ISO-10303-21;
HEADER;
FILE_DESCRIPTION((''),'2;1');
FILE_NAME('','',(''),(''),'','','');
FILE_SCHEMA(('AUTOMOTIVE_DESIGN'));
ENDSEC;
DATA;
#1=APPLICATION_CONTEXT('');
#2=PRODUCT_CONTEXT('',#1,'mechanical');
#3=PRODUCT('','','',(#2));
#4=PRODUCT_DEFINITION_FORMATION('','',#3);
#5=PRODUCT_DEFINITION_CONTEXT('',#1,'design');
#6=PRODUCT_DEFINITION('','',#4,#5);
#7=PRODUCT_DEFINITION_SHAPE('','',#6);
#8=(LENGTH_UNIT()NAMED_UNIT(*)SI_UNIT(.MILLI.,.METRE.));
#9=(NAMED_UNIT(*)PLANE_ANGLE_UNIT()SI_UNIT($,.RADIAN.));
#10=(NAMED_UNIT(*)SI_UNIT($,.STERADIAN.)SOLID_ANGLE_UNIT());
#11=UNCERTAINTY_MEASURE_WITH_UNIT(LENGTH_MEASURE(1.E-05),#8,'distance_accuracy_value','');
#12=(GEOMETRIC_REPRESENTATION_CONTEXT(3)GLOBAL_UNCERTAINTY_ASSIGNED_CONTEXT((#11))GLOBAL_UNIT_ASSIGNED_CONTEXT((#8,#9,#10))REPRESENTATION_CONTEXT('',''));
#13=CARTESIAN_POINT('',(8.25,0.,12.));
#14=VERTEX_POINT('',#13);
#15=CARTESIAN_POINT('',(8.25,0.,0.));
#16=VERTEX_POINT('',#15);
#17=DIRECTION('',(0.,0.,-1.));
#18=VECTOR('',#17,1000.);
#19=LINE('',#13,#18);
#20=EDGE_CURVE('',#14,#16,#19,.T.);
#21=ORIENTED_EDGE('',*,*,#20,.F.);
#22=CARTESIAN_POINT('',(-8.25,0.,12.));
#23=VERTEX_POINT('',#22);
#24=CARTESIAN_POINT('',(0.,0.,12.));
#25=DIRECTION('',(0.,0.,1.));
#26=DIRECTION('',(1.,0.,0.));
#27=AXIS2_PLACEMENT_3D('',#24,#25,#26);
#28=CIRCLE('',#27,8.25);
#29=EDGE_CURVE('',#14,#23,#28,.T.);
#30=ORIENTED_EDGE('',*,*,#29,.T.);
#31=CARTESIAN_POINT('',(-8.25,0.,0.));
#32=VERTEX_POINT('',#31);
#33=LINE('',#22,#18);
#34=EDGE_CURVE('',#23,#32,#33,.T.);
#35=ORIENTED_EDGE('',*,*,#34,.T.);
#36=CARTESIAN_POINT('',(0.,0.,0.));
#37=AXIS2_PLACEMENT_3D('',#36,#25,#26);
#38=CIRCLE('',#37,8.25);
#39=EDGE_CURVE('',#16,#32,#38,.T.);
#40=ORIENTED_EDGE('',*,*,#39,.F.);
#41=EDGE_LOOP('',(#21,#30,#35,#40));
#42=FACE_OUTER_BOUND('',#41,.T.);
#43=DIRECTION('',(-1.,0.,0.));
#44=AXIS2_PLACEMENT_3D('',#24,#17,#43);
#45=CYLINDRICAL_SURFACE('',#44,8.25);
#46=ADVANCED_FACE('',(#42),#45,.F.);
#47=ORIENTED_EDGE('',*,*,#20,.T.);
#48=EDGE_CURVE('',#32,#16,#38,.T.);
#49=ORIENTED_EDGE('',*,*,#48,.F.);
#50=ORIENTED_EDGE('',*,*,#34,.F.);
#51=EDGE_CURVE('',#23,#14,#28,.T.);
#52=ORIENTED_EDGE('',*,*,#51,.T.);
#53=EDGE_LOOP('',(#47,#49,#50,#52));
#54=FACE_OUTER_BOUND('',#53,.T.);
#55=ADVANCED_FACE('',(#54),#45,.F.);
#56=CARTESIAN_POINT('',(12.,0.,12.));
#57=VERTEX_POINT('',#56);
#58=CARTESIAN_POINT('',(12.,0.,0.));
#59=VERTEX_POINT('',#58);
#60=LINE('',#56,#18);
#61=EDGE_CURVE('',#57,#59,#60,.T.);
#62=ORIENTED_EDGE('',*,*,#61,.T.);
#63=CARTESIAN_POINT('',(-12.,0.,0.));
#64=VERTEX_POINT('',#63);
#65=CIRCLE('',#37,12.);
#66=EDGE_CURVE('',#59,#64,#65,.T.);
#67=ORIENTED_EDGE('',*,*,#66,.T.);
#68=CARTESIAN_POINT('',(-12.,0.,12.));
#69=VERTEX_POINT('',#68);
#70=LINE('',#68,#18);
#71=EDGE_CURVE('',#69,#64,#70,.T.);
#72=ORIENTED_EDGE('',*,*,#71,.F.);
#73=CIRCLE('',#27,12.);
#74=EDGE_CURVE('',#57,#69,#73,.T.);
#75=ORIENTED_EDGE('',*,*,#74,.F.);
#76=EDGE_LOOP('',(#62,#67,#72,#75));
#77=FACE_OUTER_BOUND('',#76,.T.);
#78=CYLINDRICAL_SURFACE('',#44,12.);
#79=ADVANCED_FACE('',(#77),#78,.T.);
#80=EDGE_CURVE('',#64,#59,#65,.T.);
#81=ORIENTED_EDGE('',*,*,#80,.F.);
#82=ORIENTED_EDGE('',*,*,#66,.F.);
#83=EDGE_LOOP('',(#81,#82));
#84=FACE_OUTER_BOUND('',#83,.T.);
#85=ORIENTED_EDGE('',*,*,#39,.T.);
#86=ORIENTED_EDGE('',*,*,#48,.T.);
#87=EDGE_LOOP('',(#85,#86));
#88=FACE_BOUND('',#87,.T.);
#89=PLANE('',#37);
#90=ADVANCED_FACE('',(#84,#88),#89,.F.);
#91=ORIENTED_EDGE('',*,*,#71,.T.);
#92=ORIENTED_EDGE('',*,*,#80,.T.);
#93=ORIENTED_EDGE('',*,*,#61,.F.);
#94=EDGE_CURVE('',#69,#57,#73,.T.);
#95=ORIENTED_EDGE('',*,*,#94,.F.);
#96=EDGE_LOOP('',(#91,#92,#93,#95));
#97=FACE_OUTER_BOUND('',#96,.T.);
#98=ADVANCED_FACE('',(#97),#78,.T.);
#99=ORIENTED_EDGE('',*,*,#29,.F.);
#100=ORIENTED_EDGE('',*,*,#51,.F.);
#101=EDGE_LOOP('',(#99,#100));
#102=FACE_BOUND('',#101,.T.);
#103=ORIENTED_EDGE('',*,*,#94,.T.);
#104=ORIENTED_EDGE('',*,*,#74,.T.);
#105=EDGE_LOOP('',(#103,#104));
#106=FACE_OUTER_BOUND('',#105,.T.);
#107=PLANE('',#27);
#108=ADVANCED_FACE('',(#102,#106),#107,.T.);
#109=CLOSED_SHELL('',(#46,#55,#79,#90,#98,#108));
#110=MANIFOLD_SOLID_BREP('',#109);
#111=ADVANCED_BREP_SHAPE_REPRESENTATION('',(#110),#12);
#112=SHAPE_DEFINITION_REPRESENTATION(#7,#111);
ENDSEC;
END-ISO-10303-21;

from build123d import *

# Parameters (mm, degrees)
SKETCH_1_R      = 12
SKETCH_1_R_2    = 8.25
EXTRUDE_1_DEPTH = 12


with BuildPart() as part:
    # 草图1 → 凸台-拉伸1 (new body)
    with BuildSketch(Plane.XY):
        Circle(SKETCH_1_R)
        Circle(SKETCH_1_R_2, mode=Mode.SUBTRACT)
    extrude(amount=EXTRUDE_1_DEPTH)


solid = part.part
